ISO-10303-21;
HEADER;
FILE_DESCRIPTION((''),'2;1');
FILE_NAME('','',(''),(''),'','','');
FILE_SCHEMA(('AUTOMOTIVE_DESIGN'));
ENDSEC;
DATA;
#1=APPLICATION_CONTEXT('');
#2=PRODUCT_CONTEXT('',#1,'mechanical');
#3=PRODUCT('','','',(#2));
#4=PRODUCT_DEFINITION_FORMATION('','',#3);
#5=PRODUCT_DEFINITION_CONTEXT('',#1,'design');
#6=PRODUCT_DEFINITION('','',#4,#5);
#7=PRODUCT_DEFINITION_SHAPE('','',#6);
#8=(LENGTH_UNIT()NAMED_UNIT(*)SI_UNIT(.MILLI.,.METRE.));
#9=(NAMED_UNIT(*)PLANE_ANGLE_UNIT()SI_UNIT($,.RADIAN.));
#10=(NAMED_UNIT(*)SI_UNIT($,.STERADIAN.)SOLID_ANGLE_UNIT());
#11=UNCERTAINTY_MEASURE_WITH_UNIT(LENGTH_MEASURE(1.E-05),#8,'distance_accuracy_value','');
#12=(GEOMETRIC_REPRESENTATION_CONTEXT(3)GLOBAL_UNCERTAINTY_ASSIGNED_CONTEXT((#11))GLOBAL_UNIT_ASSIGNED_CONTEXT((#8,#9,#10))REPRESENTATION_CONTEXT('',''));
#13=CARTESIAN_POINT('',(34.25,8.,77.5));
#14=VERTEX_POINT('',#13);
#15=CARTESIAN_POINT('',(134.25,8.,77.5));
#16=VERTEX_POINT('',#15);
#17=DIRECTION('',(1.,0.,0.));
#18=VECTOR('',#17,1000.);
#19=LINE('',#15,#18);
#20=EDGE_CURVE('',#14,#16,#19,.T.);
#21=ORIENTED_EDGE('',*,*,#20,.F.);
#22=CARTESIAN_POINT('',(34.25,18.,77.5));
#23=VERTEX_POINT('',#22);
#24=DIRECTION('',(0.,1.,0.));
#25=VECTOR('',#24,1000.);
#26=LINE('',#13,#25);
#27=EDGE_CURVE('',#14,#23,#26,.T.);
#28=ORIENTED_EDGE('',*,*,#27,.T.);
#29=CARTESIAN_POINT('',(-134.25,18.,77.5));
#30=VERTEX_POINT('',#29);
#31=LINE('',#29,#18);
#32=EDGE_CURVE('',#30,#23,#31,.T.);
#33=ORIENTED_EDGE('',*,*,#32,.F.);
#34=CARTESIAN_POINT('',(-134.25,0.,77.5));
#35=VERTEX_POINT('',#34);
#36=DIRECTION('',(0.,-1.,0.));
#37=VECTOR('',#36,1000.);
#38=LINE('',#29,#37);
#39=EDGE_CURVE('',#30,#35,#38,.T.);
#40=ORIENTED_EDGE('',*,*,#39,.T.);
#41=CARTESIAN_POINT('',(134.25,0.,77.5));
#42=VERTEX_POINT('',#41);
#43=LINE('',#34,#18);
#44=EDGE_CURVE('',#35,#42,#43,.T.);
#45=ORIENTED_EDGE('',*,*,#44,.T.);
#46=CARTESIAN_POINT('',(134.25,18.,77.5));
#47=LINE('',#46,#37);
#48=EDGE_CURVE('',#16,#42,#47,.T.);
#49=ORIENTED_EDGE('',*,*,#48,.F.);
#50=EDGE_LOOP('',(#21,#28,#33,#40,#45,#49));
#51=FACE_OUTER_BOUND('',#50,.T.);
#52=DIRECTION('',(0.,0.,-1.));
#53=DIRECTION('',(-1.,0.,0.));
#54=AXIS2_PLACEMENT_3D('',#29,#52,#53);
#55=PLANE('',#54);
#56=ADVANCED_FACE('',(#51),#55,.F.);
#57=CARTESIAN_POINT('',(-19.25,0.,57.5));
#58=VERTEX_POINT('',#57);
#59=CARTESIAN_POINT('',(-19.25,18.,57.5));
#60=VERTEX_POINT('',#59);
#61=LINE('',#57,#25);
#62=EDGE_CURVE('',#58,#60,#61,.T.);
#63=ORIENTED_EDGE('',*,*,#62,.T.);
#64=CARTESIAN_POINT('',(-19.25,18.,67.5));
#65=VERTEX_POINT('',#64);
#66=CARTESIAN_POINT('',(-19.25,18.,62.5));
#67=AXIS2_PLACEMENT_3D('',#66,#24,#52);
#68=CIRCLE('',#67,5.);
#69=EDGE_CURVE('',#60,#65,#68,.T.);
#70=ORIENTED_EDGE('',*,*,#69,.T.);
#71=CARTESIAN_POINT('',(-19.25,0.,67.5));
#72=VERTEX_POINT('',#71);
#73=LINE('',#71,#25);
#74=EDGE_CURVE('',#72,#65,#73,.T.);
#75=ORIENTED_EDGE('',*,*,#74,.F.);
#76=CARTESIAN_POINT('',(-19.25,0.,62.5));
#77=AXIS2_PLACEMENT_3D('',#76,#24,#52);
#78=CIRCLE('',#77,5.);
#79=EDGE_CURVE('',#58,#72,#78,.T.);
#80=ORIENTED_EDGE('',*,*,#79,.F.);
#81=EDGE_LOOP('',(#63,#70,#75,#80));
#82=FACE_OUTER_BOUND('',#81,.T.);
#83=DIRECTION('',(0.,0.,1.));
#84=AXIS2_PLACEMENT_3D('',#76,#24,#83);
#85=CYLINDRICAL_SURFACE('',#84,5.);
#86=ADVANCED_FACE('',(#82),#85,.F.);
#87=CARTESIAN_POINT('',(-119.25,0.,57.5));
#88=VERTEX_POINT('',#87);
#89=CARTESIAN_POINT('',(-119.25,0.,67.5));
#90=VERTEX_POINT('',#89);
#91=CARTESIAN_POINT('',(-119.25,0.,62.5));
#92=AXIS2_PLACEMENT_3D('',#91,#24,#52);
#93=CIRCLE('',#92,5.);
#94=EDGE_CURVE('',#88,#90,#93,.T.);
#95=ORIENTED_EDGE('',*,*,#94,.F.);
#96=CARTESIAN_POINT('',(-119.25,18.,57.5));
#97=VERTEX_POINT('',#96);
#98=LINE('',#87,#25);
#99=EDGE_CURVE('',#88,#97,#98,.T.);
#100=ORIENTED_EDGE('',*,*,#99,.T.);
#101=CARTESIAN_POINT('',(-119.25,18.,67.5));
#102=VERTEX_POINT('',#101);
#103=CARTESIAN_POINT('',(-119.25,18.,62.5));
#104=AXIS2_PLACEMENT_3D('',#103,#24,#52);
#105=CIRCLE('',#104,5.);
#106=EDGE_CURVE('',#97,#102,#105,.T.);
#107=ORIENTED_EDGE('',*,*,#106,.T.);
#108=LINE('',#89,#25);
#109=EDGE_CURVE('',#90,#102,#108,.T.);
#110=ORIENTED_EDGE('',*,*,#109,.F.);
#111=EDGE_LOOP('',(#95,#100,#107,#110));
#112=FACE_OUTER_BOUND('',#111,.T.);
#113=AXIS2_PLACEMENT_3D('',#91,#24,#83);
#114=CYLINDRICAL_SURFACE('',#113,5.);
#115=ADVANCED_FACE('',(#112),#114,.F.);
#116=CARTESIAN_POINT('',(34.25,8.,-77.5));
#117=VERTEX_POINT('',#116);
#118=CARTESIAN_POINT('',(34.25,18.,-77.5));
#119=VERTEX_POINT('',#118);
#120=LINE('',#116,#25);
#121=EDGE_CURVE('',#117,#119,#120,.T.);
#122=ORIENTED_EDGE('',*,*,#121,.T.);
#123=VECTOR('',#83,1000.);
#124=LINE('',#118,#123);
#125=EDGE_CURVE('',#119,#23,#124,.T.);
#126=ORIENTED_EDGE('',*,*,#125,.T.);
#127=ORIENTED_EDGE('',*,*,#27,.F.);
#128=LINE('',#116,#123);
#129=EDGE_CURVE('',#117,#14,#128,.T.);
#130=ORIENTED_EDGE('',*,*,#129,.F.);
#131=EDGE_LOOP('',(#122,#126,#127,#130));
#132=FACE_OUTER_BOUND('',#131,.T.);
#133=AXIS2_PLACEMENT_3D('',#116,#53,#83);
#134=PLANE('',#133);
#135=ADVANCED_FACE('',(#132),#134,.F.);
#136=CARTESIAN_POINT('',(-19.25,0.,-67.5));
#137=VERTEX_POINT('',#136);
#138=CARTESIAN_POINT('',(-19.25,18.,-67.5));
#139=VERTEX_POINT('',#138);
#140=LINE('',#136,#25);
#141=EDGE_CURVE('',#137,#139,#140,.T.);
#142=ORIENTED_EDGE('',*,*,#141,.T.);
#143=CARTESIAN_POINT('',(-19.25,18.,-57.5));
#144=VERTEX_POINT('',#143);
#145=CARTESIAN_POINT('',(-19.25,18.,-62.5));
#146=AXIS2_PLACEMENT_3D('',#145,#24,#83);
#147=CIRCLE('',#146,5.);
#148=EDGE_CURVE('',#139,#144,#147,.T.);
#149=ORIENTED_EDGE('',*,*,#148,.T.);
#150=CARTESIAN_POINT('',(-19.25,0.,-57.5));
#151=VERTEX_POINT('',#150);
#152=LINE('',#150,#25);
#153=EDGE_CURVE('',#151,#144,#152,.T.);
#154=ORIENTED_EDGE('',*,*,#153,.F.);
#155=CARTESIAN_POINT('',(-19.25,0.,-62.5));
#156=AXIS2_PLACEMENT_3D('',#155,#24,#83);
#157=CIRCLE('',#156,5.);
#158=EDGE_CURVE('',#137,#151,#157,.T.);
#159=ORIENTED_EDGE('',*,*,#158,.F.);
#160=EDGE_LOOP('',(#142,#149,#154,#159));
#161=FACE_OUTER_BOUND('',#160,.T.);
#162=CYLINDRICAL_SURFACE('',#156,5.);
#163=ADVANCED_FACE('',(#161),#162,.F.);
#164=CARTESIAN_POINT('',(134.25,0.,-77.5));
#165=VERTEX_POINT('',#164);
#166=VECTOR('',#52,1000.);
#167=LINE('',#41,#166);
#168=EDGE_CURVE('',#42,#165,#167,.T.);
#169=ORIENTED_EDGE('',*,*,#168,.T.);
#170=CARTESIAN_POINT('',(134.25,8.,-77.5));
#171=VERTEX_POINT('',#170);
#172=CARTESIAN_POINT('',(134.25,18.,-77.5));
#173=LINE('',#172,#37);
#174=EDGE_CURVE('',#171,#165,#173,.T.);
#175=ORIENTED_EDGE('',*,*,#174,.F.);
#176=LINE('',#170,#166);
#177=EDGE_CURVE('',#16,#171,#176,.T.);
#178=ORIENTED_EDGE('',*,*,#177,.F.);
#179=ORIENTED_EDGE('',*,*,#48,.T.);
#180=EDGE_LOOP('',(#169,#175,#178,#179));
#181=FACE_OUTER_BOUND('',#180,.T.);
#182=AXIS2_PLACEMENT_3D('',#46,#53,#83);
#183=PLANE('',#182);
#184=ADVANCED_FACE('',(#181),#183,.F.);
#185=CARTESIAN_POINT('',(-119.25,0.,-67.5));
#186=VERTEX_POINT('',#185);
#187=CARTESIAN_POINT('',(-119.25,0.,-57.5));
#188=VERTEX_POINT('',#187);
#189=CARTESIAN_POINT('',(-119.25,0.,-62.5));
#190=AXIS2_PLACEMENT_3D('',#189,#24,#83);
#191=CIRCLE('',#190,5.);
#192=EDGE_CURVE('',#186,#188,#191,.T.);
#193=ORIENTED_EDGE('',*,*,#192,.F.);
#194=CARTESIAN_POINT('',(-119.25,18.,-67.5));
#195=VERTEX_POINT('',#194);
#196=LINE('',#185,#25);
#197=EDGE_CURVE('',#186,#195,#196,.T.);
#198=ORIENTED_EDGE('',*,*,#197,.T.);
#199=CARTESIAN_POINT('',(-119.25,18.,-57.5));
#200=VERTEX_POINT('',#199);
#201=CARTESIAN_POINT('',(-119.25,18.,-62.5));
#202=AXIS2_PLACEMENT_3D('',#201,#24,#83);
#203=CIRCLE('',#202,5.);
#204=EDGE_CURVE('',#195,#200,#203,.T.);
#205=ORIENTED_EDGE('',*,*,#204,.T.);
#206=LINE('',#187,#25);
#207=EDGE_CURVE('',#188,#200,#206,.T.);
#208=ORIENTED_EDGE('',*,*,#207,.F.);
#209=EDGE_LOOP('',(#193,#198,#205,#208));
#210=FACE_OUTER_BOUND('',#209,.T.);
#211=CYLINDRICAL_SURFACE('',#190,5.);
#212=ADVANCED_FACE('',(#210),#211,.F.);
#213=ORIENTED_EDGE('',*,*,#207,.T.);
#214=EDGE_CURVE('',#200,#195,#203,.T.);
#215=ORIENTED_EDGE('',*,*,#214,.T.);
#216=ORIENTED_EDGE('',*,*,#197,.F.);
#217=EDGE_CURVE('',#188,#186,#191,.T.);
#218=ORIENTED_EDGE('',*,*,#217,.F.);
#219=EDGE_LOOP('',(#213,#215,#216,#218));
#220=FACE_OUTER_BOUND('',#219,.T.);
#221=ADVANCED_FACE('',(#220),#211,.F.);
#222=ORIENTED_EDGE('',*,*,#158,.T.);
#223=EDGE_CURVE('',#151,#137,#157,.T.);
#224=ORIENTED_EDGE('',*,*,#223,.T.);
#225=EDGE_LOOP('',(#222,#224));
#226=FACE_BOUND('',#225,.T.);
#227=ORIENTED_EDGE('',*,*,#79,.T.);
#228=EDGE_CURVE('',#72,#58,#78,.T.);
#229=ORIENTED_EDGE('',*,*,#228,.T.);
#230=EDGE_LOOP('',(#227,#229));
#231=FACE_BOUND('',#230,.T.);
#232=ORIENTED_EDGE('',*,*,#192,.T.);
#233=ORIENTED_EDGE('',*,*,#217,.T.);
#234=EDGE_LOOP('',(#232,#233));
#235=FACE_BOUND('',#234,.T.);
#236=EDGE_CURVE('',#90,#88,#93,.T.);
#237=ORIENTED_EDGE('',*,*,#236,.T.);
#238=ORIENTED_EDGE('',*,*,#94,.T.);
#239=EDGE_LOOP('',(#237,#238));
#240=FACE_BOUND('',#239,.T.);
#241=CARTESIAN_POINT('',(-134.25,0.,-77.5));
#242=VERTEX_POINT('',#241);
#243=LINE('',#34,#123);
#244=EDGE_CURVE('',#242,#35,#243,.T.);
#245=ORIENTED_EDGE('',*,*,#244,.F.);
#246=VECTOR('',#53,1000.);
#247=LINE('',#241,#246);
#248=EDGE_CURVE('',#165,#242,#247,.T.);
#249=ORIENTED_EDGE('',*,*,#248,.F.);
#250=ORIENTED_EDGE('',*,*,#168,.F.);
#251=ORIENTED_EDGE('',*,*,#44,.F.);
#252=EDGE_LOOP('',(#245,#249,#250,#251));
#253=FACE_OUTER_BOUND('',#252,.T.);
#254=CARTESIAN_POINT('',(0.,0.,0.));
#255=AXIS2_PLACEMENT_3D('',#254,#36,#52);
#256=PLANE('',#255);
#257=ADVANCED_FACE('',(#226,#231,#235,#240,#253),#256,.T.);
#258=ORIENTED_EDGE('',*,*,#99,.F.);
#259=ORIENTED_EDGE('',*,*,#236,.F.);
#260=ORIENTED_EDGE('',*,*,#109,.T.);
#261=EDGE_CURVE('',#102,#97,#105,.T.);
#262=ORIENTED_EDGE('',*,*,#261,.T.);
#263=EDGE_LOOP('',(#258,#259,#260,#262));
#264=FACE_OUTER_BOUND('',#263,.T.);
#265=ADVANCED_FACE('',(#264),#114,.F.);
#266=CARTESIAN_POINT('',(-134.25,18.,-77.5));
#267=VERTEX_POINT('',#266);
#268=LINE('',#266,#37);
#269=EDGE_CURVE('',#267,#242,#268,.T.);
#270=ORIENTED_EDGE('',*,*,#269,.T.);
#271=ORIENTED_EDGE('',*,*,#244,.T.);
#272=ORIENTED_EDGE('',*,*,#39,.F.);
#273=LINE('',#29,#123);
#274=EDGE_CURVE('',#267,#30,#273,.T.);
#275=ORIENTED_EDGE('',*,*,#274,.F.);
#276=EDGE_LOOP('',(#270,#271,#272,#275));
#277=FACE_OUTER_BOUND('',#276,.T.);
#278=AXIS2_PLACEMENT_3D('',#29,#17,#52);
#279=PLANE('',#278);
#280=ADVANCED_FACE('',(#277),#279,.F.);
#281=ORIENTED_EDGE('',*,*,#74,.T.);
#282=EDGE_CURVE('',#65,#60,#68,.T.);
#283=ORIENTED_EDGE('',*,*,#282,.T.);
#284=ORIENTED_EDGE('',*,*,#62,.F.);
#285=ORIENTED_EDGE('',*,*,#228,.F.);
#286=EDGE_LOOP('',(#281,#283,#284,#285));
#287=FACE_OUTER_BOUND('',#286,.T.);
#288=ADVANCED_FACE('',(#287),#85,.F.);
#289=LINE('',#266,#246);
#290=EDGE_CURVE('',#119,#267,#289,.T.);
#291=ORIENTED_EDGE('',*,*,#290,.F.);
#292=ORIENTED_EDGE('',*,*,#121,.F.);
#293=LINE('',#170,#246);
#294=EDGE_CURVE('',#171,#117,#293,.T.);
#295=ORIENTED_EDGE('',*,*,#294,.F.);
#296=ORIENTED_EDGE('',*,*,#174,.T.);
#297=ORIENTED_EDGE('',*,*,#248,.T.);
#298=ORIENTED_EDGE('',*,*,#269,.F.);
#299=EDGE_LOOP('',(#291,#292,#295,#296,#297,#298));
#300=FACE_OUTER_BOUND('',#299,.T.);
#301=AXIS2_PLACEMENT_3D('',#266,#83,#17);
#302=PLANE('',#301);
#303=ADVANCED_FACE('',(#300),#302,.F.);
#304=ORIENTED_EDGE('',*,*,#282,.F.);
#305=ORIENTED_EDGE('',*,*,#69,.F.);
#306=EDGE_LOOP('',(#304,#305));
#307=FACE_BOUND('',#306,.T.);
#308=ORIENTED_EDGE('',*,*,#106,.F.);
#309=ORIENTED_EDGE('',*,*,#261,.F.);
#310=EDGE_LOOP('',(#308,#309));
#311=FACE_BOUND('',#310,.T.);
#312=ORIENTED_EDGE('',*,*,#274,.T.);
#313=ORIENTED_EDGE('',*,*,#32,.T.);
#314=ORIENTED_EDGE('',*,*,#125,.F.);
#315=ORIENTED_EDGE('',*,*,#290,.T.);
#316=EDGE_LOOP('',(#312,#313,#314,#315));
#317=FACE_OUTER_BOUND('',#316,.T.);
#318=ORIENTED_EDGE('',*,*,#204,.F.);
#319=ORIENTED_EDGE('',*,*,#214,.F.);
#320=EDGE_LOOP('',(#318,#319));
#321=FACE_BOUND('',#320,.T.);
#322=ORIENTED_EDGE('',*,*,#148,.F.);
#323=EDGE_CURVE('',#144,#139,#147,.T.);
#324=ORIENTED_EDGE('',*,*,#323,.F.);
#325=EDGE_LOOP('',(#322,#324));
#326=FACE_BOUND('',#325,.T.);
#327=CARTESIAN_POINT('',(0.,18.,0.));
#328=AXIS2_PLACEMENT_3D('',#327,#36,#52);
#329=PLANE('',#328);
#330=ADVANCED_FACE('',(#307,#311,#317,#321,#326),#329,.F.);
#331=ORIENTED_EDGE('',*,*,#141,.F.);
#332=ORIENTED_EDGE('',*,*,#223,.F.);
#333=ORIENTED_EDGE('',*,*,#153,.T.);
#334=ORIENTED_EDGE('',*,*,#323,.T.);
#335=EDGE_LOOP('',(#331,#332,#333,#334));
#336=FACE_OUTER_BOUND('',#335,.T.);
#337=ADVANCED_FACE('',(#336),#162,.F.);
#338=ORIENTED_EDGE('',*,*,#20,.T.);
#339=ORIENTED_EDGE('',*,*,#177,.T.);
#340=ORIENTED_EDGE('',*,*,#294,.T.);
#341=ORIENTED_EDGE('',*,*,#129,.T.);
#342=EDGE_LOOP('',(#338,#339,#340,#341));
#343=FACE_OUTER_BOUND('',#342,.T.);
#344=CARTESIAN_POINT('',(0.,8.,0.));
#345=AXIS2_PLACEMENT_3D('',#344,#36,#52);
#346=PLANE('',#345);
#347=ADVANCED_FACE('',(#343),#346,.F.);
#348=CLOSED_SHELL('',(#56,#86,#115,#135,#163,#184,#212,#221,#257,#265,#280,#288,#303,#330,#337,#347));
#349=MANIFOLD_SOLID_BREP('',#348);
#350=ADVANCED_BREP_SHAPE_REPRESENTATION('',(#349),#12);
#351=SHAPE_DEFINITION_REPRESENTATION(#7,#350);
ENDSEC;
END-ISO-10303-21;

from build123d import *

# Parameters (mm, degrees)
SKETCH1_W           = 268.5
SKETCH1_H           = 155
BOSS_EXTRUDE1_DEPTH = 18
SKETCH2_R           = 5
CUT_EXTRUDE1_DEPTH  = 18
SKETCH3_W           = 100
SKETCH3_H           = 155
CUT_EXTRUDE2_DEPTH  = 10


with BuildPart() as part:
    # Sketch1 → Boss-Extrude1 (new body)
    with BuildSketch(Plane(origin=(0, 0, 0), x_dir=(1, 0, 0), z_dir=(0, 1, 0))):
        Rectangle(SKETCH1_W, SKETCH1_H)
    extrude(amount=BOSS_EXTRUDE1_DEPTH)

    # Sketch2 → Cut-Extrude1 (cut)
    with BuildSketch(Plane(origin=(0, 18, 0), x_dir=(1, 0, 0), z_dir=(0, 1, 0))):
        with Locations(Location((-119.25, 62.5, 0), (0, 0, 270))):
            Circle(SKETCH2_R)
        with Locations(Location((-19.25, 62.5, 0), (0, 0, 270))):
            Circle(SKETCH2_R)
        with Locations(Location((-19.25, -62.5, 0), (0, 0, 90))):
            Circle(SKETCH2_R)
        with Locations(Location((-119.25, -62.5, 0), (0, 0, 90))):
            Circle(SKETCH2_R)
    extrude(amount=-CUT_EXTRUDE1_DEPTH, mode=Mode.SUBTRACT)

    # Sketch3 → Cut-Extrude2 (cut)
    with BuildSketch(Plane(origin=(0, 18, 0), x_dir=(1, 0, 0), z_dir=(0, 1, 0))):
        with Locations((84.25, 0)):
            Rectangle(SKETCH3_W, SKETCH3_H)
    extrude(amount=-CUT_EXTRUDE2_DEPTH, mode=Mode.SUBTRACT)


solid = part.part
